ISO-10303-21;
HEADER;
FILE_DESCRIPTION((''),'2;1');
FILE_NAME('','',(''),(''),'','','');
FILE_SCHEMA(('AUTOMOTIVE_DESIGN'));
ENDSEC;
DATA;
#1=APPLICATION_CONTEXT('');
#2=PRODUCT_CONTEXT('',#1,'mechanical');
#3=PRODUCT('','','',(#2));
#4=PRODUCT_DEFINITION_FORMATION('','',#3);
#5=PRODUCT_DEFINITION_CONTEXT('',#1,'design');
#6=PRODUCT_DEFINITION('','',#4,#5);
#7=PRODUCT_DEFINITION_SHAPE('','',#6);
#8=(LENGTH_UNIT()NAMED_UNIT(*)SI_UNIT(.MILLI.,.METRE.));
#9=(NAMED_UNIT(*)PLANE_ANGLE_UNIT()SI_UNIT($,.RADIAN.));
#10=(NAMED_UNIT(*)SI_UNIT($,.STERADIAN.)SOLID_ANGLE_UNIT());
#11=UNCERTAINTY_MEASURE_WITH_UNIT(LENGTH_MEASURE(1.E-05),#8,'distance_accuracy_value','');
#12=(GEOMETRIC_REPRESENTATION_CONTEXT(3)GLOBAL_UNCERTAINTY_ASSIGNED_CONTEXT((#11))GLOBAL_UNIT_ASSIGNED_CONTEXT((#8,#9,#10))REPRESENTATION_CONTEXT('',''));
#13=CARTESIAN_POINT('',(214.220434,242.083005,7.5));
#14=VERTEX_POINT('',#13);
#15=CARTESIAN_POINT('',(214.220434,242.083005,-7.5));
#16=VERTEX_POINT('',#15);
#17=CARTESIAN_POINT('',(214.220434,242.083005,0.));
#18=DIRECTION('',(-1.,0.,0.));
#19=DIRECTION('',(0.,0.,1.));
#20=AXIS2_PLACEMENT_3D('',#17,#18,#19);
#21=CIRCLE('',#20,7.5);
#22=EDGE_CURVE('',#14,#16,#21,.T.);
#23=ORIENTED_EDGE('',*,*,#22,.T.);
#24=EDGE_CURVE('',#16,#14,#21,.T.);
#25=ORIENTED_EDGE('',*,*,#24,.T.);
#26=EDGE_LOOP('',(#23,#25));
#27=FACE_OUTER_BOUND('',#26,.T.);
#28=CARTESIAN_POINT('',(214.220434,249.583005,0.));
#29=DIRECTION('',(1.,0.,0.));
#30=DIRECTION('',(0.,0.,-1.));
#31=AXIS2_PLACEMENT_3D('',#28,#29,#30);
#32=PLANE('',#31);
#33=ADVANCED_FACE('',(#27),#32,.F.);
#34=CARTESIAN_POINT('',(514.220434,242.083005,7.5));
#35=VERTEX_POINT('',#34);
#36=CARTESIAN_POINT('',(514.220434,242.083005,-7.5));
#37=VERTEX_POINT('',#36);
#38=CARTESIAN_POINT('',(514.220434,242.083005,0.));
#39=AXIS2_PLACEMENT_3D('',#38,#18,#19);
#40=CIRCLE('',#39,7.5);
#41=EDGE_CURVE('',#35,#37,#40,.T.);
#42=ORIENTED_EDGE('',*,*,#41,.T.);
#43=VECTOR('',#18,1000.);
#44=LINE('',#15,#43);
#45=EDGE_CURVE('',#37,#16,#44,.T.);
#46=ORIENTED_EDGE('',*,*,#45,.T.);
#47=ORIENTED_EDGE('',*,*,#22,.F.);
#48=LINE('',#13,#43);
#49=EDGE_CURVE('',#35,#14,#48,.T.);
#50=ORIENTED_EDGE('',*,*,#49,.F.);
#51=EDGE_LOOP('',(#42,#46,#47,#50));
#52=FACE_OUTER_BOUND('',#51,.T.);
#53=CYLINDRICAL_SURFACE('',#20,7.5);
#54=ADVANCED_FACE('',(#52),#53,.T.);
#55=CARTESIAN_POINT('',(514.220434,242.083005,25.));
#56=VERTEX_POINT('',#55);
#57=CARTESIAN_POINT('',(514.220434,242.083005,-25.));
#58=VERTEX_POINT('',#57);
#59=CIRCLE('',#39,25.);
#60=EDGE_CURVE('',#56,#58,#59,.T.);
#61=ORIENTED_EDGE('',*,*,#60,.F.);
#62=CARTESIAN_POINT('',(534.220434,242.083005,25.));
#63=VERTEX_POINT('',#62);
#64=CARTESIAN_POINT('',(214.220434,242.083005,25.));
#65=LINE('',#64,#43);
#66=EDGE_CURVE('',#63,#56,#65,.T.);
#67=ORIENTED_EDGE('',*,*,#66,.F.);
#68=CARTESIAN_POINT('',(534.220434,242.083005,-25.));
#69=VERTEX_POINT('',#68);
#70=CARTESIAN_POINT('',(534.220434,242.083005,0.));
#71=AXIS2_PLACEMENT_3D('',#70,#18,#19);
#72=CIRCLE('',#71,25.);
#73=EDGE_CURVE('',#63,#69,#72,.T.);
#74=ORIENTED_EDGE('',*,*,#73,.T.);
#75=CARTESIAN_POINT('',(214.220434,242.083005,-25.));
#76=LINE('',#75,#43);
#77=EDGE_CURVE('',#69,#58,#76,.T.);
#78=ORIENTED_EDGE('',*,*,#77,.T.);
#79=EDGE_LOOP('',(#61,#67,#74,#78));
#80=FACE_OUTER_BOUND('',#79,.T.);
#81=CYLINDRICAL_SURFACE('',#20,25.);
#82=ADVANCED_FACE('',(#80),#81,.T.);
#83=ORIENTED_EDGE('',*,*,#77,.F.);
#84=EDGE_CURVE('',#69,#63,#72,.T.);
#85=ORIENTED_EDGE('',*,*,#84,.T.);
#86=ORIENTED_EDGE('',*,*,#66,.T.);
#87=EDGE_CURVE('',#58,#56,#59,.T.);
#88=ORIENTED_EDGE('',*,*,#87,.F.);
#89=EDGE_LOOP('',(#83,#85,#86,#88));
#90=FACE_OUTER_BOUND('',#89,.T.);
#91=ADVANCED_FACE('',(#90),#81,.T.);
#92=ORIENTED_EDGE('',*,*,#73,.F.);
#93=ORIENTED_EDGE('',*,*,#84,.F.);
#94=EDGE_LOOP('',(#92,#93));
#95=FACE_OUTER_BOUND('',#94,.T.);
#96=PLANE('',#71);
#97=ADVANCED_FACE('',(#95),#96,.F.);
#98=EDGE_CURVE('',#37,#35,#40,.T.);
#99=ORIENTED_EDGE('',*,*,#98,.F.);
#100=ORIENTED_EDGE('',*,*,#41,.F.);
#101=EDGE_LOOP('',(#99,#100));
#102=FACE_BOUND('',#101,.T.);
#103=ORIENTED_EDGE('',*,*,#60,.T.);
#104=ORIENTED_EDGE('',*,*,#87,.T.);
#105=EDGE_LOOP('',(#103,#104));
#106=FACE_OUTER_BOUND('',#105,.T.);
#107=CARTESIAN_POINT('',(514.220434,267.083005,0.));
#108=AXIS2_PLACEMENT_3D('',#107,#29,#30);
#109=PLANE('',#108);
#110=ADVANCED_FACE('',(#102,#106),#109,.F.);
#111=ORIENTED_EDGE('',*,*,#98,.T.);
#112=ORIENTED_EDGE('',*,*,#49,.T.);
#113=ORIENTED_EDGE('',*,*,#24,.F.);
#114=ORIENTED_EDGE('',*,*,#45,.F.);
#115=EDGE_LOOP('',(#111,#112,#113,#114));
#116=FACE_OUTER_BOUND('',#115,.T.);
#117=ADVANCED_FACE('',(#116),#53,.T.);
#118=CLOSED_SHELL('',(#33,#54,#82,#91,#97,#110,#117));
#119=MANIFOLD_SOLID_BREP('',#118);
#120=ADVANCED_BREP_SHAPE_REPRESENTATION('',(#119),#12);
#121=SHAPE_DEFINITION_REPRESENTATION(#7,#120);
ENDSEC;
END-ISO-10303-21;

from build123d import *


with BuildPart() as part:
    # Sketch1 → Revolve1 (revolve)
    with BuildSketch(Plane.XY, mode=Mode.PRIVATE) as revolve1_sk:
        Polygon((214.220434241, 242.08300471), (534.220434241, 242.08300471), (534.220434241, 267.08300471), (514.220434241, 267.08300471), (514.220434241, 249.58300471), (214.220434241, 249.58300471), align=None)
    revolve(revolve1_sk.sketch.rotate(Axis((214.220434241, 242.08300471, 0), (1, 0, 0)), 90), axis=Axis((214.220434241, 242.08300471, 0), (1, 0, 0)))


solid = part.part
